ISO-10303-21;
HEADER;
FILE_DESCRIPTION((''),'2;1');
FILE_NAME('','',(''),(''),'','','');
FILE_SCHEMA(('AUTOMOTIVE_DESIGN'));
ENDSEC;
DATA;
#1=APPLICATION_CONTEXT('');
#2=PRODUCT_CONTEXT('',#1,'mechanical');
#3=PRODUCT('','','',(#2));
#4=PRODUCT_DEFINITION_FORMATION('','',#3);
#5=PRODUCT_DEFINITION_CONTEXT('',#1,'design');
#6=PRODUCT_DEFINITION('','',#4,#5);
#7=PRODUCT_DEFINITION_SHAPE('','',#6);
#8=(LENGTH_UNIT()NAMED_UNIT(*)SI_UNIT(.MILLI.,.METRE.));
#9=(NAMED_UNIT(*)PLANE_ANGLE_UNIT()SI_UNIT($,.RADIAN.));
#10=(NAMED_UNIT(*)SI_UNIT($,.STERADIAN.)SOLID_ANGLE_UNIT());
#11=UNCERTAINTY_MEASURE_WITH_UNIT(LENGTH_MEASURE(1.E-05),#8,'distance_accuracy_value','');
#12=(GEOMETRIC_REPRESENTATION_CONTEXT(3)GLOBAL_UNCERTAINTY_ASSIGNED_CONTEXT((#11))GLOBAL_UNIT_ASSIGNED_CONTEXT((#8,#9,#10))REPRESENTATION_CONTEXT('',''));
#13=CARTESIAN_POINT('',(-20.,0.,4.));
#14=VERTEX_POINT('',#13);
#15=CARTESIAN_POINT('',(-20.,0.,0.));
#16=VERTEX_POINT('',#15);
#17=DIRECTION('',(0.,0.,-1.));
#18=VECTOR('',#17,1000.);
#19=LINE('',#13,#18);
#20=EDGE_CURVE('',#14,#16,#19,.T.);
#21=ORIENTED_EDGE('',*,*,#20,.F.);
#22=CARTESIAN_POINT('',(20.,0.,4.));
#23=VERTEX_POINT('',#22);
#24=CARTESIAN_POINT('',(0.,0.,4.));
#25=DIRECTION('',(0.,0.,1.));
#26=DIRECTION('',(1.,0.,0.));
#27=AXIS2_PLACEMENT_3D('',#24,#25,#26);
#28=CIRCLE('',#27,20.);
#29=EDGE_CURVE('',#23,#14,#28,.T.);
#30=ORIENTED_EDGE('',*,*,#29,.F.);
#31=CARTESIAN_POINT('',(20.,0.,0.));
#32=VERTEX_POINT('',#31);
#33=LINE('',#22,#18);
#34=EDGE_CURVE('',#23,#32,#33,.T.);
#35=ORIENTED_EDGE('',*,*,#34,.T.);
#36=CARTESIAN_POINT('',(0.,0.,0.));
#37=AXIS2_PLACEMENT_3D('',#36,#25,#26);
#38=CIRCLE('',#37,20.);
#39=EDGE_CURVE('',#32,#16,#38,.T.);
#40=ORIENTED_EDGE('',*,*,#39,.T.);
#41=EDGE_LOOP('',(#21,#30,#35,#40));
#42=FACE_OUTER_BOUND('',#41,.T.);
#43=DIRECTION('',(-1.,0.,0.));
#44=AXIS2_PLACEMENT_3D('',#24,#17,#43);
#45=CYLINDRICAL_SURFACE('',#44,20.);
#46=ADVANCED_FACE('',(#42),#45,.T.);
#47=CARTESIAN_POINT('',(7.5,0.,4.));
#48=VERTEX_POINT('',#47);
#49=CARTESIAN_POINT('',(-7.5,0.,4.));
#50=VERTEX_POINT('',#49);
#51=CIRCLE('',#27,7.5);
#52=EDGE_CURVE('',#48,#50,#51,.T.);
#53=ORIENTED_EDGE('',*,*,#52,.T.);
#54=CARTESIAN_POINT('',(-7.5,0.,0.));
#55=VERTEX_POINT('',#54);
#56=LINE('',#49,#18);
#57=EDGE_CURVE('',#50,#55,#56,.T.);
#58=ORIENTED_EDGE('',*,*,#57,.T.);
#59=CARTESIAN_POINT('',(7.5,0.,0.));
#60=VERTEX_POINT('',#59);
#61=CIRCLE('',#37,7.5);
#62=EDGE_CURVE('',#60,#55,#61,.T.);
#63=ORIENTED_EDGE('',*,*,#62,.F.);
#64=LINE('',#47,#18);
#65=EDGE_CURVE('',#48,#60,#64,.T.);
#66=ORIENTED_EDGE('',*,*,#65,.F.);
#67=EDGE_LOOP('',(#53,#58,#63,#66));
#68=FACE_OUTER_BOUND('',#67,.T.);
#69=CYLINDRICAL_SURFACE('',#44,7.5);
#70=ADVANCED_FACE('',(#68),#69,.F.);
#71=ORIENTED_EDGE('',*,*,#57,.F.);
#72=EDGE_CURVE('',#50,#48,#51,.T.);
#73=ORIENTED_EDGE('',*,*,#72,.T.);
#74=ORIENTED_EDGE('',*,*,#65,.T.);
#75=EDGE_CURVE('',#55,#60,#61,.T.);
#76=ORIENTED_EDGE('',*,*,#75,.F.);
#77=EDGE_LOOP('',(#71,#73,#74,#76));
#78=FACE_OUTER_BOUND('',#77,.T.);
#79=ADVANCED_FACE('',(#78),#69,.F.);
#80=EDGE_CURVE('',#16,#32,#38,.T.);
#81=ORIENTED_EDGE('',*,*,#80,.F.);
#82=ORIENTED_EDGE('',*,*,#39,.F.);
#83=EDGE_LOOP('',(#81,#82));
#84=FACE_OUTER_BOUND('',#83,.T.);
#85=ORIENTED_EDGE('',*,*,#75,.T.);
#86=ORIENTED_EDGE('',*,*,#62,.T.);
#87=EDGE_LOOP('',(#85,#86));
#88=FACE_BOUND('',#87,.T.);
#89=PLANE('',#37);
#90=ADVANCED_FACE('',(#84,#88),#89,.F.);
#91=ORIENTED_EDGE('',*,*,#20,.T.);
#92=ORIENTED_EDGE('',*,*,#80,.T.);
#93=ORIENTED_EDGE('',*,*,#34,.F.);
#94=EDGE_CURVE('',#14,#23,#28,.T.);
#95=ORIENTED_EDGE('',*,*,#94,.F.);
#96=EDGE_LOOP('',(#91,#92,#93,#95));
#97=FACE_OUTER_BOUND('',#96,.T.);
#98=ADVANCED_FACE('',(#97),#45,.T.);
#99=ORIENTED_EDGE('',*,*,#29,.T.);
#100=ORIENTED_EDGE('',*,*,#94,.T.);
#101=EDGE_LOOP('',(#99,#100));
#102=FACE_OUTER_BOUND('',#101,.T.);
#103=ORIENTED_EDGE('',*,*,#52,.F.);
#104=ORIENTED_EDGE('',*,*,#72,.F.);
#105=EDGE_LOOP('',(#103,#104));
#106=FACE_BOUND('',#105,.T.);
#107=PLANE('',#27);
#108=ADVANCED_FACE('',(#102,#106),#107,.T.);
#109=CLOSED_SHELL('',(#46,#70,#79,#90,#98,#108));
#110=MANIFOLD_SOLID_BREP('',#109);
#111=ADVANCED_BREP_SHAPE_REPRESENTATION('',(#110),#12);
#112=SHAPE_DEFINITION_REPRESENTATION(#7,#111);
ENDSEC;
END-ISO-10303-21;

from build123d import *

# Parameters (mm, degrees)
SKETCH1_R           = 20
SKETCH1_R_2         = 7.5
BOSS_EXTRUDE1_DEPTH = 4


with BuildPart() as part:
    # Sketch1 → Boss-Extrude1 (new body)
    with BuildSketch(Plane.XY):
        Circle(SKETCH1_R)
        Circle(SKETCH1_R_2, mode=Mode.SUBTRACT)
    extrude(amount=BOSS_EXTRUDE1_DEPTH)


solid = part.part
